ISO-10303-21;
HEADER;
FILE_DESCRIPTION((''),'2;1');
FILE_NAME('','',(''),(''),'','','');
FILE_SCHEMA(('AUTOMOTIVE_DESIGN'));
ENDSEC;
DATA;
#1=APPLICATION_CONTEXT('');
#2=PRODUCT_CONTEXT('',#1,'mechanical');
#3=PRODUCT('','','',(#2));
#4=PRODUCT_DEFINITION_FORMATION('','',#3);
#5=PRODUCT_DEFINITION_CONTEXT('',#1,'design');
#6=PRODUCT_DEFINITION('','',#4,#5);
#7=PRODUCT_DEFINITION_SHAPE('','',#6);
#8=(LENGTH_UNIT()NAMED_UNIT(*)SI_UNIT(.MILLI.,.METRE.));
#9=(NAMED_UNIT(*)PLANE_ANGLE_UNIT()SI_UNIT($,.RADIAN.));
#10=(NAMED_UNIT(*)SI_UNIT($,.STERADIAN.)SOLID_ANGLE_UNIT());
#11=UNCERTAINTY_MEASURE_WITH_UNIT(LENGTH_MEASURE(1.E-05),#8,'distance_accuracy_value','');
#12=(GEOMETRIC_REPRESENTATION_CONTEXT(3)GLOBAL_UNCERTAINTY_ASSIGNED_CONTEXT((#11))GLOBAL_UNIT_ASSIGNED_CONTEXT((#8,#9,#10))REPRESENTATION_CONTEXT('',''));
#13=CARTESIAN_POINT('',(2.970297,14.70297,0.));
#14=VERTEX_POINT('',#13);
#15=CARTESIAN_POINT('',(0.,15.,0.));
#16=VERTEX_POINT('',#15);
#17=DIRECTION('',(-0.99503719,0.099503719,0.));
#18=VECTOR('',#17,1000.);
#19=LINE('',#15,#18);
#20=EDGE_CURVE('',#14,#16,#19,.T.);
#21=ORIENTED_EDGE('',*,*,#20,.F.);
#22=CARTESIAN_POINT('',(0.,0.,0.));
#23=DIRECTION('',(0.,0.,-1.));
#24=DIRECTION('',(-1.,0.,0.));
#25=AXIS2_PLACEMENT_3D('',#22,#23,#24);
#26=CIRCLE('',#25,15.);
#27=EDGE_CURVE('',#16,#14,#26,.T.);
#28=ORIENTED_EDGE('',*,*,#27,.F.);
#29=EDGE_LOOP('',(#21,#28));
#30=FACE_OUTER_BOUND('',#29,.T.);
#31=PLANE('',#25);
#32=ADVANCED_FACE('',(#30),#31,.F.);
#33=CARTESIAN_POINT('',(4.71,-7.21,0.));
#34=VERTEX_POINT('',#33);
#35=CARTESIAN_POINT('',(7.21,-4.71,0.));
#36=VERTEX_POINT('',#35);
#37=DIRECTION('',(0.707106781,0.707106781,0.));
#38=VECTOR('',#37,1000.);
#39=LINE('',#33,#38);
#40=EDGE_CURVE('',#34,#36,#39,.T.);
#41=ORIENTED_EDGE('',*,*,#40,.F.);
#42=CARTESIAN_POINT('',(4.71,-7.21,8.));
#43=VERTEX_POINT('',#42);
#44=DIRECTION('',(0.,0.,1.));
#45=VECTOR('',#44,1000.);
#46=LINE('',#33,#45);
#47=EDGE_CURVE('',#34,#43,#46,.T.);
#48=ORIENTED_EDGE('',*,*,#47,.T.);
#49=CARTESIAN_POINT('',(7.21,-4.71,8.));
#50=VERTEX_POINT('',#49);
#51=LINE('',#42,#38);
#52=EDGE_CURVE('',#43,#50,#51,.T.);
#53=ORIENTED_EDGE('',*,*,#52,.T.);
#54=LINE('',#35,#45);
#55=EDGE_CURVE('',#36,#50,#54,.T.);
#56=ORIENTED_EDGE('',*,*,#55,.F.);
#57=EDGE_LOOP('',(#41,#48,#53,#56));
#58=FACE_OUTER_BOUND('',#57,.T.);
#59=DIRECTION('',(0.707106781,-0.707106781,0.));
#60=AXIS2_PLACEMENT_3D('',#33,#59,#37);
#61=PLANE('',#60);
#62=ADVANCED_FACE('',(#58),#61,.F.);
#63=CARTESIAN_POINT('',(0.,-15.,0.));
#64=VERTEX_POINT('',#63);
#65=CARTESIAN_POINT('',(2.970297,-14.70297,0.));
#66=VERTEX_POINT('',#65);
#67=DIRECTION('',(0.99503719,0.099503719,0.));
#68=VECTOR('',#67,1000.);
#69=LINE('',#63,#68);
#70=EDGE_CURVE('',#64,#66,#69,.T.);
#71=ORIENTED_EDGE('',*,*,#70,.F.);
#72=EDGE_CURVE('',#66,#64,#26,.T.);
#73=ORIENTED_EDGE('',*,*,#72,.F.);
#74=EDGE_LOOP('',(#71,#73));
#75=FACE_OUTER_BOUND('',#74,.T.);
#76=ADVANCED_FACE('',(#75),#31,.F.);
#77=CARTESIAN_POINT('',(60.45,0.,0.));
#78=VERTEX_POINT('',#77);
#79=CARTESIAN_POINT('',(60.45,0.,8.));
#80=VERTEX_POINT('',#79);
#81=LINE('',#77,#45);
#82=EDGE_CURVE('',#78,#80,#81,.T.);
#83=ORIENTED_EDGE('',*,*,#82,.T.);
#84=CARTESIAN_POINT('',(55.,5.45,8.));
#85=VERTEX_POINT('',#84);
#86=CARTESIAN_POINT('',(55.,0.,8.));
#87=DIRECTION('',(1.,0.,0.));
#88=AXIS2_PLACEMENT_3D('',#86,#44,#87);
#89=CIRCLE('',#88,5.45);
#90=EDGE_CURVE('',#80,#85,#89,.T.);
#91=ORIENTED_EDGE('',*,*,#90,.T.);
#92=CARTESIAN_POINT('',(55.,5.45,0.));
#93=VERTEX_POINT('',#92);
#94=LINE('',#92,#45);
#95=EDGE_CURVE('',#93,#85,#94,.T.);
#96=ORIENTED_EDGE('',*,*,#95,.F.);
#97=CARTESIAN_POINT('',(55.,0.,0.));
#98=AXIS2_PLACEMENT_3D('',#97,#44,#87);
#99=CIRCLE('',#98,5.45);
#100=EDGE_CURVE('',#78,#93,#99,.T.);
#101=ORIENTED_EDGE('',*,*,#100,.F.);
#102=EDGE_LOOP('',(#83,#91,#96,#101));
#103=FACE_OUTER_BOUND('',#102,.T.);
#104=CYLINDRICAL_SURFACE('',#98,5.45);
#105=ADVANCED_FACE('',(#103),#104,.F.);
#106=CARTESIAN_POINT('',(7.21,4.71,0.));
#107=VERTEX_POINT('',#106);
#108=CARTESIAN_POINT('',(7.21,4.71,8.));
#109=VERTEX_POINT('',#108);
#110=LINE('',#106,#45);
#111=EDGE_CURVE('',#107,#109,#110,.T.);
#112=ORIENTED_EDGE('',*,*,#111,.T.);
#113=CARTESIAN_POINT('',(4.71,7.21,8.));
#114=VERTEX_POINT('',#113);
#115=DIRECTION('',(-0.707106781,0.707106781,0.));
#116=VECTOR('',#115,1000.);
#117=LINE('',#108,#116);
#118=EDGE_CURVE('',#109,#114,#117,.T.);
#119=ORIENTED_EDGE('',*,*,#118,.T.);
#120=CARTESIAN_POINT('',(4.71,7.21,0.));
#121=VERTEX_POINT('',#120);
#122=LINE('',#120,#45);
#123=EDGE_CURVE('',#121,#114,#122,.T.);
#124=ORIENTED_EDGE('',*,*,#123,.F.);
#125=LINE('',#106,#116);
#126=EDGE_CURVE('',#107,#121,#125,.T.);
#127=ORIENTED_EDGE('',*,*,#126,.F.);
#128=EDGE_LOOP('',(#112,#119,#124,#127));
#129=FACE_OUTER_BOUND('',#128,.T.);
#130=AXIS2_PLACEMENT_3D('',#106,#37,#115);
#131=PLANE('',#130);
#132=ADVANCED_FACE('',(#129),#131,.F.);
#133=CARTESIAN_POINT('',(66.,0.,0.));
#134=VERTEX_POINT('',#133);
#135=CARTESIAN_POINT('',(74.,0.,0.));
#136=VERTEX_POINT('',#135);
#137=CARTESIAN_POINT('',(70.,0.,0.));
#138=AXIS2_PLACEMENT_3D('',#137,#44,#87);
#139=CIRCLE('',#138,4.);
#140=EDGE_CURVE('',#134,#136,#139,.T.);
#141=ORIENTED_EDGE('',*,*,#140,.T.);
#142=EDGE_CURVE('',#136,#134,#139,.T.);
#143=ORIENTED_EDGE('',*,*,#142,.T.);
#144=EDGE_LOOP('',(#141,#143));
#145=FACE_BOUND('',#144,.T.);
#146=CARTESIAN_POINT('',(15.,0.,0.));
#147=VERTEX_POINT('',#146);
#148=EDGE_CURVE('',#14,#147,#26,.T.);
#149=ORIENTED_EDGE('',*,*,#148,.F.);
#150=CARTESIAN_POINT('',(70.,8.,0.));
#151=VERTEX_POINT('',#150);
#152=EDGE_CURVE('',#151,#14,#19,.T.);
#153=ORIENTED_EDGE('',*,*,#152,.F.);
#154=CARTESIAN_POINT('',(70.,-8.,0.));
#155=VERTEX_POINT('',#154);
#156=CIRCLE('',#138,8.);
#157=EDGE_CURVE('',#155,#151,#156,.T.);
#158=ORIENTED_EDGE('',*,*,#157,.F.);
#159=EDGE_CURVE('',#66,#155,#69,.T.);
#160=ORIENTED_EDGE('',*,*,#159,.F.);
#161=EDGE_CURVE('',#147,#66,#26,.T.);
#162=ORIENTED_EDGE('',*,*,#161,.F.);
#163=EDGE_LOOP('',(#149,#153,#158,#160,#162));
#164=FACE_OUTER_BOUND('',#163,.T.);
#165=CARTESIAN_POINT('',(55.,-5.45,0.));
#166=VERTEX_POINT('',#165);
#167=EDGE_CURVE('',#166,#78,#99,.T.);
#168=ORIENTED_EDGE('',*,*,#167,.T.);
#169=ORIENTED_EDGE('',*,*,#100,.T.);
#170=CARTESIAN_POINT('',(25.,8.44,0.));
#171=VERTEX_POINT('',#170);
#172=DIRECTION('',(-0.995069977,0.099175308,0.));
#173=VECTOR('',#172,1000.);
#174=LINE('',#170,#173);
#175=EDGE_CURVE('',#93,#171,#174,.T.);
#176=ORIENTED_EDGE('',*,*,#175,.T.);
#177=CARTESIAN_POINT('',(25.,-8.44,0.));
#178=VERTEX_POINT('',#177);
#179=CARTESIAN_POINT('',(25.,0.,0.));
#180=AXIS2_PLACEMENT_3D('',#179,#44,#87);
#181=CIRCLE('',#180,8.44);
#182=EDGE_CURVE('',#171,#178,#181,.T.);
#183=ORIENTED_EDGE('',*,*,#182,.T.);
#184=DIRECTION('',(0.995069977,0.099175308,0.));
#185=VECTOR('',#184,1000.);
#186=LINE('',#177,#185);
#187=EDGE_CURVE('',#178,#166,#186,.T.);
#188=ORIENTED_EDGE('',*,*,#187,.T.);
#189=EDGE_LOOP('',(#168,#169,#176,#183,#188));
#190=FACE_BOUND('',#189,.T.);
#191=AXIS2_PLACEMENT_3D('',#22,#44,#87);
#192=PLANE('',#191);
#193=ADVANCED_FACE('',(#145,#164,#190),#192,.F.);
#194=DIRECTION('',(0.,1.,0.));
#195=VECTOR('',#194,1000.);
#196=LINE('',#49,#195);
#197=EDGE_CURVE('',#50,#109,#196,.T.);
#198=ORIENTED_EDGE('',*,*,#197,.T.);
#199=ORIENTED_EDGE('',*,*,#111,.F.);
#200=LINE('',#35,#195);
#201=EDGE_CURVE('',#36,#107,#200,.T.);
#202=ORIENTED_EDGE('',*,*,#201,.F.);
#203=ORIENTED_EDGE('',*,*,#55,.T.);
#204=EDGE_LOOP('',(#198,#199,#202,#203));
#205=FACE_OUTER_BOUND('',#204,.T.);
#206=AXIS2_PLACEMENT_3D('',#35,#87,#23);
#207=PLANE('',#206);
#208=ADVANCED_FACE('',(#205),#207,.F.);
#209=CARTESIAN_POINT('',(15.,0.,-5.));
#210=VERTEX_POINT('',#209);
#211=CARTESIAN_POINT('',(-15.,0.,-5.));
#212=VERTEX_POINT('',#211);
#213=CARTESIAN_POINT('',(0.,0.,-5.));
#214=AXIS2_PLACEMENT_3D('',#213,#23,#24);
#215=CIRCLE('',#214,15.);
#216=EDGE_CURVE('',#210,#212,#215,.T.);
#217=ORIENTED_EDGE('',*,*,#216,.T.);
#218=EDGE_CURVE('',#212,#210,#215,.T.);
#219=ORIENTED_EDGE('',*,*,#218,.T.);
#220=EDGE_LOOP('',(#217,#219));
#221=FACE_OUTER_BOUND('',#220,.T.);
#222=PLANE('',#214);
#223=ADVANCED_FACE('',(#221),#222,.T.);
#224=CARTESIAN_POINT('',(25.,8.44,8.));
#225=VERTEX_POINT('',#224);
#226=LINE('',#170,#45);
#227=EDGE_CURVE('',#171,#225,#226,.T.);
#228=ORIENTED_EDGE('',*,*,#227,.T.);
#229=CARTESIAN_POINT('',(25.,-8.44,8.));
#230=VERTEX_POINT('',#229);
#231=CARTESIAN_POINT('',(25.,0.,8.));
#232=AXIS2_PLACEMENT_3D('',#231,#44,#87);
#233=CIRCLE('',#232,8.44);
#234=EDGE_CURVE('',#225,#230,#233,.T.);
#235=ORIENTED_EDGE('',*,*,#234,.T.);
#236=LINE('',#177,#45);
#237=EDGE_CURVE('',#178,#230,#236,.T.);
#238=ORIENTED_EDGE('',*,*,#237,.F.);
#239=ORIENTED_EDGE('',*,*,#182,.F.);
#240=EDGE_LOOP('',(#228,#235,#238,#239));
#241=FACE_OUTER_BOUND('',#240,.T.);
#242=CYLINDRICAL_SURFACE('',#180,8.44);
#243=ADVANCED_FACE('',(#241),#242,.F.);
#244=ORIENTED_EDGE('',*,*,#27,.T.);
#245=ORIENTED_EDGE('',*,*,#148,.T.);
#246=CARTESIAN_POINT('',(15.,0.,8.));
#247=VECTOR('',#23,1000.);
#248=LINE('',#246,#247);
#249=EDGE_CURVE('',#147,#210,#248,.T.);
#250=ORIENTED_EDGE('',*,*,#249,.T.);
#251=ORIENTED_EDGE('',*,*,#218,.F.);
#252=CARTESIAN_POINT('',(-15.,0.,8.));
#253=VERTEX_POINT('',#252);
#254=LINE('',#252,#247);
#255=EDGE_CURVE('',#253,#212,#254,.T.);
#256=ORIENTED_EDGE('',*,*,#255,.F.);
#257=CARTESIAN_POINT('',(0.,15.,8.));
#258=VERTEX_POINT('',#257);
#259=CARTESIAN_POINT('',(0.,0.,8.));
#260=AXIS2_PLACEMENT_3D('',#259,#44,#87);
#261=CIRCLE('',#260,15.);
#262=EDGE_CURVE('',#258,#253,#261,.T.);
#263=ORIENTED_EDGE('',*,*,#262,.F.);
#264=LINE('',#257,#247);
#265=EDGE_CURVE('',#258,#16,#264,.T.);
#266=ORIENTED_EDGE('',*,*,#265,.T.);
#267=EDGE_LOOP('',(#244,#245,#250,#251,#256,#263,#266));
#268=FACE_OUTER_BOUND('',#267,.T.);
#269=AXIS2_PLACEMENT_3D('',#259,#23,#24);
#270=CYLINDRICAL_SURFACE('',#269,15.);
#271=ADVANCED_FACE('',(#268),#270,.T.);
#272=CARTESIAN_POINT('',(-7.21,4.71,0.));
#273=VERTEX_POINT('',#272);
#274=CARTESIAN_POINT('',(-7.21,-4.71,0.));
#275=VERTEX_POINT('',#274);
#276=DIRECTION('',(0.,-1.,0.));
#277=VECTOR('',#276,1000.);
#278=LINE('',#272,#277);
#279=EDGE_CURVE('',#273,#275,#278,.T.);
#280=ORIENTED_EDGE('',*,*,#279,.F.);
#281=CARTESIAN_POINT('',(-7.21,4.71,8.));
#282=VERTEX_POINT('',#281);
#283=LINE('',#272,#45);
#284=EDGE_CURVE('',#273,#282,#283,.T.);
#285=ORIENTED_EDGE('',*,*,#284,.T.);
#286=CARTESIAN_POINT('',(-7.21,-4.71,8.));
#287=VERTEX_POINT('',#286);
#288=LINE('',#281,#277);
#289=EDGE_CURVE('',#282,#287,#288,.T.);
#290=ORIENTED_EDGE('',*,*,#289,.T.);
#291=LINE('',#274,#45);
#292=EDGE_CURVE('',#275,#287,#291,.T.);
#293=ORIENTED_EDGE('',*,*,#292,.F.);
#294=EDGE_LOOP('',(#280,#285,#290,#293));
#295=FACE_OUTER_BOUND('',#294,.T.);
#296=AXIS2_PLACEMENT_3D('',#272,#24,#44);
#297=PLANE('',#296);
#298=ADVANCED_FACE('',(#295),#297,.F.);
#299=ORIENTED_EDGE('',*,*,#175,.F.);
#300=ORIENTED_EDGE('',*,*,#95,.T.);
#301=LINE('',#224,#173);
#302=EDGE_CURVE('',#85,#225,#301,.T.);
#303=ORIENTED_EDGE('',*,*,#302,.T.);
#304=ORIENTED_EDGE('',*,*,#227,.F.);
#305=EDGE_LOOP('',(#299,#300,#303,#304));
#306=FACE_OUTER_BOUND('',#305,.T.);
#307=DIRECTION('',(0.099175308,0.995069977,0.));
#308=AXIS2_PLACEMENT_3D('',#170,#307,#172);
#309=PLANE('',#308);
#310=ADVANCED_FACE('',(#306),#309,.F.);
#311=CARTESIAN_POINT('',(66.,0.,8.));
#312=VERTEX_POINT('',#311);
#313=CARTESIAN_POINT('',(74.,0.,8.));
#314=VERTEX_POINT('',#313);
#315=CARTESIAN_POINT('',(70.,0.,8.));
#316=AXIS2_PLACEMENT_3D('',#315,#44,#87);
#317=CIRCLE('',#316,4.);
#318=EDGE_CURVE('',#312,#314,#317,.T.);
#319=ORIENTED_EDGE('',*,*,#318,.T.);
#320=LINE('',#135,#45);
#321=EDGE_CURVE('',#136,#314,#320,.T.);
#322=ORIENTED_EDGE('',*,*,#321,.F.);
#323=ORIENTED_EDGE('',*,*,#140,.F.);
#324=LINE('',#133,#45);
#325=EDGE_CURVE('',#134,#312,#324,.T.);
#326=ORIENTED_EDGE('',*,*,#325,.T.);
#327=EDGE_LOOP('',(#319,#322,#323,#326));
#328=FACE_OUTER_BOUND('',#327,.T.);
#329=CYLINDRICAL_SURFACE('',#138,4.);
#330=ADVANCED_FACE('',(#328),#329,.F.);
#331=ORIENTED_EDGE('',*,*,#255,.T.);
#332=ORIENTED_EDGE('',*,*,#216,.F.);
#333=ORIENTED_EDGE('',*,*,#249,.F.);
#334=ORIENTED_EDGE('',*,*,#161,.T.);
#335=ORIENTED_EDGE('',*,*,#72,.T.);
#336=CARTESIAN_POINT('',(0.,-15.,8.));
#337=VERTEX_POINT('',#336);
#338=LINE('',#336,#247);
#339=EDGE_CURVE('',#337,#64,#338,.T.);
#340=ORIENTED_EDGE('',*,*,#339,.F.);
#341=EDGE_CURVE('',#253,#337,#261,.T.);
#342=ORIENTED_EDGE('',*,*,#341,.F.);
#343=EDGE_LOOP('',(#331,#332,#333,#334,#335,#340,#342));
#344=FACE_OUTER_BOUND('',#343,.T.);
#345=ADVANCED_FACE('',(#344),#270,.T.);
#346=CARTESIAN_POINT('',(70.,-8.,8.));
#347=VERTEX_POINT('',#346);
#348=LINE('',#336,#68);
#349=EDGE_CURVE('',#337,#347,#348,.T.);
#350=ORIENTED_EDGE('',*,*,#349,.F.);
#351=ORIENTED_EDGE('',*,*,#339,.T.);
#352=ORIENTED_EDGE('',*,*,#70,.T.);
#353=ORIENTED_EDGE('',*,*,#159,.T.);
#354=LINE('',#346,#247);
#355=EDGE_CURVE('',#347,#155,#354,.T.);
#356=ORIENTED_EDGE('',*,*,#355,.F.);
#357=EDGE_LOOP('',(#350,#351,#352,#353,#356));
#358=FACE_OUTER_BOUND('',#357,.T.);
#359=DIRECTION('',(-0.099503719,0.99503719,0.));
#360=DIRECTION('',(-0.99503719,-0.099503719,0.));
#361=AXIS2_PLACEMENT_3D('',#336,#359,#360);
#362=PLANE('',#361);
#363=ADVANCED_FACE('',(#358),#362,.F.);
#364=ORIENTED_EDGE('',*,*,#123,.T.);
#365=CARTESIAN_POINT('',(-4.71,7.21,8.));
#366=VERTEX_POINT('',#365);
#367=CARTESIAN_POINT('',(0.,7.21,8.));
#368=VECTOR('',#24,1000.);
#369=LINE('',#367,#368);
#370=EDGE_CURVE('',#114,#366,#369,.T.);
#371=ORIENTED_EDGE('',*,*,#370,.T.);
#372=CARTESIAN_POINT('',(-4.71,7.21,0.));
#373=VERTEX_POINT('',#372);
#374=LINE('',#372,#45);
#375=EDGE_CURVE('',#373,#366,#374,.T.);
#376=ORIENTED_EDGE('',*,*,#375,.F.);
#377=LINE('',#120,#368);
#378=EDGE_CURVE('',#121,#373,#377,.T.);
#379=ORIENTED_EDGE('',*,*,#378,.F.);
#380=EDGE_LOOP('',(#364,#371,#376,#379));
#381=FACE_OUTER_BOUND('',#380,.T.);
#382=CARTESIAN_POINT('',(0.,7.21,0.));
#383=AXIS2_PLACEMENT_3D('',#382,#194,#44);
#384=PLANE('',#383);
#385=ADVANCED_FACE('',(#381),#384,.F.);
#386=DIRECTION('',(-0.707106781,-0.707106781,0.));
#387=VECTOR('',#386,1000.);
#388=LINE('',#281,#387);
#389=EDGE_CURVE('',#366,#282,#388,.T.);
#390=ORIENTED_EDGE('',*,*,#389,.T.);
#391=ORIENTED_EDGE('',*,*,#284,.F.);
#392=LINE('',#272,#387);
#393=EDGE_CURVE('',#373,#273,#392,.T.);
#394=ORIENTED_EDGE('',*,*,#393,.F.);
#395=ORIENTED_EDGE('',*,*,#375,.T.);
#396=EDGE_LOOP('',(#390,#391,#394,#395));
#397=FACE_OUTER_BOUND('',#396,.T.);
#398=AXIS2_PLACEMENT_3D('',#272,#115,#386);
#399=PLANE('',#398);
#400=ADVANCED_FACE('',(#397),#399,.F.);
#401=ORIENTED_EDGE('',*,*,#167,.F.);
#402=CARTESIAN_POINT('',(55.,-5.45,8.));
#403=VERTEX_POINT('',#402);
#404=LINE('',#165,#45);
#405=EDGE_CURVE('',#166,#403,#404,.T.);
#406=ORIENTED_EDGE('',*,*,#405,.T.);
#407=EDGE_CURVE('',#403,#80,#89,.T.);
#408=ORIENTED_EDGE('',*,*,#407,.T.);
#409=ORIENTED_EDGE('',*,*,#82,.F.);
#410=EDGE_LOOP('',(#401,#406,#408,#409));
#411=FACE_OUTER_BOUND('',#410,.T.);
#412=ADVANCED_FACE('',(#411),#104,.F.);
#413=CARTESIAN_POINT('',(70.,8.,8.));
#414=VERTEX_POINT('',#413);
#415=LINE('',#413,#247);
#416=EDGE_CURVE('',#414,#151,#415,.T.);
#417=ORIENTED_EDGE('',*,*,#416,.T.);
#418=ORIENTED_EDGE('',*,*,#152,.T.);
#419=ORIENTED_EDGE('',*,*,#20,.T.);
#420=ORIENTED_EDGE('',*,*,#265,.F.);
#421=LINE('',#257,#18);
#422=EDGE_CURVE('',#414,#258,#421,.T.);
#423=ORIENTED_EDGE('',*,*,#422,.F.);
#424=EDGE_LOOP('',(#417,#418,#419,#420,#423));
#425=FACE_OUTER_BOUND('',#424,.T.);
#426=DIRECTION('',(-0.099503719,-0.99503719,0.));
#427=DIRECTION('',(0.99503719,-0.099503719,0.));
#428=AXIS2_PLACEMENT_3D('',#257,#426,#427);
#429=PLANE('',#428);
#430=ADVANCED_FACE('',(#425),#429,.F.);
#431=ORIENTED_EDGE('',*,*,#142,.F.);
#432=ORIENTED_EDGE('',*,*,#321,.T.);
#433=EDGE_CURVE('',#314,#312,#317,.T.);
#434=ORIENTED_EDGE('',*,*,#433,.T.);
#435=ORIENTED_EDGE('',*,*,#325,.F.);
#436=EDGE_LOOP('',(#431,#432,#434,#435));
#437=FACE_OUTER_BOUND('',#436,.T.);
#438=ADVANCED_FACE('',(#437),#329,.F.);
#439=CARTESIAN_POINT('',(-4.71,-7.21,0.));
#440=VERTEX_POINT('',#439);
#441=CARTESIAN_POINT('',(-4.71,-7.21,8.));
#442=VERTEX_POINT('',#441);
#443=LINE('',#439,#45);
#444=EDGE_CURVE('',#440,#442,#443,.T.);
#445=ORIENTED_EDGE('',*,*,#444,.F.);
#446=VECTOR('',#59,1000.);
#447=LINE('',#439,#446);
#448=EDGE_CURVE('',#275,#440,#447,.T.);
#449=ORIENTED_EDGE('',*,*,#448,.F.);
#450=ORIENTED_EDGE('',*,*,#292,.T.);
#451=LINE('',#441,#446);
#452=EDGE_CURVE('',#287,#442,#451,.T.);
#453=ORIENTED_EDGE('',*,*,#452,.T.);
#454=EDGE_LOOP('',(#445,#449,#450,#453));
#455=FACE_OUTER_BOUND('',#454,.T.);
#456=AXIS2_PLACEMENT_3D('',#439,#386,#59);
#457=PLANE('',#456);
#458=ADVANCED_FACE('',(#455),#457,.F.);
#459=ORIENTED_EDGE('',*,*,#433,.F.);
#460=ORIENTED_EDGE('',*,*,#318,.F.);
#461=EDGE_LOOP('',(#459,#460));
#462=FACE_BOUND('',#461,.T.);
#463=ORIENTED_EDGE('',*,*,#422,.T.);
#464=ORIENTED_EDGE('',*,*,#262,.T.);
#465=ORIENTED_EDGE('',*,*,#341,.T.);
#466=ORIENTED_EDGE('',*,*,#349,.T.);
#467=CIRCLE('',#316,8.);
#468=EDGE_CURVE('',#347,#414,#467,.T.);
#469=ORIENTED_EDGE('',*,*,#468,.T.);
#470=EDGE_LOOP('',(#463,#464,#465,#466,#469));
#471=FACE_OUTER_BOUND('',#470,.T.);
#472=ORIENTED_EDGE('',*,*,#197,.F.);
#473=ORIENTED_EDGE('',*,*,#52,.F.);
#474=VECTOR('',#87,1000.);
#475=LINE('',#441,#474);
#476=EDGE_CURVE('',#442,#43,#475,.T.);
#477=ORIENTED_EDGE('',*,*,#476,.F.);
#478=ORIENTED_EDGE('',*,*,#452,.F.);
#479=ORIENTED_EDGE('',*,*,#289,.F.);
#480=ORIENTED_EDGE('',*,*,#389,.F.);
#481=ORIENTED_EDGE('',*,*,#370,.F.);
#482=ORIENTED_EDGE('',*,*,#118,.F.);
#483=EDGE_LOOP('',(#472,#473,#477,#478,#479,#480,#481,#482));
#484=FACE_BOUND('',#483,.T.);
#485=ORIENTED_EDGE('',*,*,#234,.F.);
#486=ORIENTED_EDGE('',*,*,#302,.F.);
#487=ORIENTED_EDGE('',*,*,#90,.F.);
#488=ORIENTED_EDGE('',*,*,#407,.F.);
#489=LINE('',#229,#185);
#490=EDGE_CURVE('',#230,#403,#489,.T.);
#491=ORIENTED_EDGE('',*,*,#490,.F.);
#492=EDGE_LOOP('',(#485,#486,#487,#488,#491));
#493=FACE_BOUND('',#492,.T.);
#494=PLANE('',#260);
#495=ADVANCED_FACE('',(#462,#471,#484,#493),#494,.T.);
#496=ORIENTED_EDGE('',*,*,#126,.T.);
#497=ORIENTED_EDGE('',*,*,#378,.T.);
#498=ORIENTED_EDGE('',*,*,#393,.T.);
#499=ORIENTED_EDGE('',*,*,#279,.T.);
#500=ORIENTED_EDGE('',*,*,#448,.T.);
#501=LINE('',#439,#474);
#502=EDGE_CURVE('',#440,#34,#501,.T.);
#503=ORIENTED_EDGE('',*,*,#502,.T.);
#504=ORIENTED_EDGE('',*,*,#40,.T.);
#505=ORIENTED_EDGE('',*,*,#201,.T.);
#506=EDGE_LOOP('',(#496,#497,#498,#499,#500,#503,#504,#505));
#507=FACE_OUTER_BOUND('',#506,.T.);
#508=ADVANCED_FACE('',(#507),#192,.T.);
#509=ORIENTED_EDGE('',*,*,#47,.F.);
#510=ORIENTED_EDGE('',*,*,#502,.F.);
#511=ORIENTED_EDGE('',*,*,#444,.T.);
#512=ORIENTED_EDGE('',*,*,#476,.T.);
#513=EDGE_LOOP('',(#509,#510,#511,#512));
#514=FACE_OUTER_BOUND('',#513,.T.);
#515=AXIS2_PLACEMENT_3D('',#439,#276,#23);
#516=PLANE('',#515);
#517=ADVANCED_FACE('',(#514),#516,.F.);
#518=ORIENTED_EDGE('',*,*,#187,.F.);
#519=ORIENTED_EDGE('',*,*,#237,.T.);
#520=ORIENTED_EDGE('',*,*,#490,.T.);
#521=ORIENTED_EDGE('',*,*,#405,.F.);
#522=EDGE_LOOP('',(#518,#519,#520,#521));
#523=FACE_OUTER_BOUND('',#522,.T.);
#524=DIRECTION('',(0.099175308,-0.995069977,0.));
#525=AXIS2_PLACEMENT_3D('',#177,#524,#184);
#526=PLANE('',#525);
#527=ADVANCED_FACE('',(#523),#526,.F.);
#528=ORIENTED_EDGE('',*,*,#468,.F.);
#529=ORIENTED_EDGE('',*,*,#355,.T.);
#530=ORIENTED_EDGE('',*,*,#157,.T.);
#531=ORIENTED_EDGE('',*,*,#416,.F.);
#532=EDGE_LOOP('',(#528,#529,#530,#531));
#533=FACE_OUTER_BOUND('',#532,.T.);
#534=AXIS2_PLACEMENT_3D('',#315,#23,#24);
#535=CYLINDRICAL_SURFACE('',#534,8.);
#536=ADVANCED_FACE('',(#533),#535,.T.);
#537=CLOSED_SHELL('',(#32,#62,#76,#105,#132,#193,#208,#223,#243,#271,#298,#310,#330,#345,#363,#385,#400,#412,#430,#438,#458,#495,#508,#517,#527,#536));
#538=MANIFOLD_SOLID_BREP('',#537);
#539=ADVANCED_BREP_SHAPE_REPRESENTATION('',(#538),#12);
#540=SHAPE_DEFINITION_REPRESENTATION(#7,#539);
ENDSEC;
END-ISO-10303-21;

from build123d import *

# Parameters (mm, degrees)
LEVER_ARM_PLATE_DEPTH  = 8
TAPERED_SLOT_CUT_DEPTH = 8
HUB_START              = 5
HUB_BOSS_SKETCH_R      = 15
HUB_BOSS_DEPTH         = 5
PIN_HOLE_SKETCH_R      = 4
PIN_HOLE_DEPTH         = 8
HEX_SOCKET_CUT_DEPTH   = 8


with BuildPart() as part:
    # Lever Profile Sketch → Lever Arm Plate (new body)
    with BuildSketch(Plane.XY):
        with BuildLine():
            Line((0, 15), (70, 8))
            ThreePointArc((70, 8), (78, 0), (70, -8))
            Line((70, -8), (0, -15))
            ThreePointArc((0, -15), (-15, 0), (0, 15))
        make_face()
    extrude(amount=LEVER_ARM_PLATE_DEPTH)

    # Tapered Slot Sketch → Tapered Slot Cut (cut)
    with BuildSketch(Plane.XY.offset(8)):
        with BuildLine():
            Line((25, 8.44), (55, 5.45))
            ThreePointArc((55, 5.45), (60.45, 0), (55, -5.45))
            Line((55, -5.45), (25, -8.44))
            ThreePointArc((25, -8.44), (16.56, 0), (25, 8.44))
        make_face()
    extrude(amount=-TAPERED_SLOT_CUT_DEPTH, mode=Mode.SUBTRACT)

    # Hub Boss Sketch → Hub Boss (add)
    with BuildSketch(Plane(origin=(0, 0, 0), x_dir=(-1, 0, 0), z_dir=(0, 0, -1)).offset(HUB_START)):
        Circle(HUB_BOSS_SKETCH_R)
    extrude(amount=-HUB_BOSS_DEPTH)

    # Pin Hole Sketch → Pin Hole (cut)
    with BuildSketch(Plane.XY.offset(8)):
        with Locations((70, 0)):
            Circle(PIN_HOLE_SKETCH_R)
    extrude(amount=-PIN_HOLE_DEPTH, mode=Mode.SUBTRACT)

    # Hex Socket Sketch → Hex Socket Cut (cut)
    with BuildSketch(Plane.XY.offset(8)):
        Polygon((0, 7.21), (-4.71, 7.21), (-7.21, 4.71), (-7.21, -4.71), (-4.71, -7.21), (4.71, -7.21), (7.21, -4.71), (7.21, 4.71), (4.71, 7.21), align=None)
    extrude(amount=-HEX_SOCKET_CUT_DEPTH, mode=Mode.SUBTRACT)


solid = part.part
